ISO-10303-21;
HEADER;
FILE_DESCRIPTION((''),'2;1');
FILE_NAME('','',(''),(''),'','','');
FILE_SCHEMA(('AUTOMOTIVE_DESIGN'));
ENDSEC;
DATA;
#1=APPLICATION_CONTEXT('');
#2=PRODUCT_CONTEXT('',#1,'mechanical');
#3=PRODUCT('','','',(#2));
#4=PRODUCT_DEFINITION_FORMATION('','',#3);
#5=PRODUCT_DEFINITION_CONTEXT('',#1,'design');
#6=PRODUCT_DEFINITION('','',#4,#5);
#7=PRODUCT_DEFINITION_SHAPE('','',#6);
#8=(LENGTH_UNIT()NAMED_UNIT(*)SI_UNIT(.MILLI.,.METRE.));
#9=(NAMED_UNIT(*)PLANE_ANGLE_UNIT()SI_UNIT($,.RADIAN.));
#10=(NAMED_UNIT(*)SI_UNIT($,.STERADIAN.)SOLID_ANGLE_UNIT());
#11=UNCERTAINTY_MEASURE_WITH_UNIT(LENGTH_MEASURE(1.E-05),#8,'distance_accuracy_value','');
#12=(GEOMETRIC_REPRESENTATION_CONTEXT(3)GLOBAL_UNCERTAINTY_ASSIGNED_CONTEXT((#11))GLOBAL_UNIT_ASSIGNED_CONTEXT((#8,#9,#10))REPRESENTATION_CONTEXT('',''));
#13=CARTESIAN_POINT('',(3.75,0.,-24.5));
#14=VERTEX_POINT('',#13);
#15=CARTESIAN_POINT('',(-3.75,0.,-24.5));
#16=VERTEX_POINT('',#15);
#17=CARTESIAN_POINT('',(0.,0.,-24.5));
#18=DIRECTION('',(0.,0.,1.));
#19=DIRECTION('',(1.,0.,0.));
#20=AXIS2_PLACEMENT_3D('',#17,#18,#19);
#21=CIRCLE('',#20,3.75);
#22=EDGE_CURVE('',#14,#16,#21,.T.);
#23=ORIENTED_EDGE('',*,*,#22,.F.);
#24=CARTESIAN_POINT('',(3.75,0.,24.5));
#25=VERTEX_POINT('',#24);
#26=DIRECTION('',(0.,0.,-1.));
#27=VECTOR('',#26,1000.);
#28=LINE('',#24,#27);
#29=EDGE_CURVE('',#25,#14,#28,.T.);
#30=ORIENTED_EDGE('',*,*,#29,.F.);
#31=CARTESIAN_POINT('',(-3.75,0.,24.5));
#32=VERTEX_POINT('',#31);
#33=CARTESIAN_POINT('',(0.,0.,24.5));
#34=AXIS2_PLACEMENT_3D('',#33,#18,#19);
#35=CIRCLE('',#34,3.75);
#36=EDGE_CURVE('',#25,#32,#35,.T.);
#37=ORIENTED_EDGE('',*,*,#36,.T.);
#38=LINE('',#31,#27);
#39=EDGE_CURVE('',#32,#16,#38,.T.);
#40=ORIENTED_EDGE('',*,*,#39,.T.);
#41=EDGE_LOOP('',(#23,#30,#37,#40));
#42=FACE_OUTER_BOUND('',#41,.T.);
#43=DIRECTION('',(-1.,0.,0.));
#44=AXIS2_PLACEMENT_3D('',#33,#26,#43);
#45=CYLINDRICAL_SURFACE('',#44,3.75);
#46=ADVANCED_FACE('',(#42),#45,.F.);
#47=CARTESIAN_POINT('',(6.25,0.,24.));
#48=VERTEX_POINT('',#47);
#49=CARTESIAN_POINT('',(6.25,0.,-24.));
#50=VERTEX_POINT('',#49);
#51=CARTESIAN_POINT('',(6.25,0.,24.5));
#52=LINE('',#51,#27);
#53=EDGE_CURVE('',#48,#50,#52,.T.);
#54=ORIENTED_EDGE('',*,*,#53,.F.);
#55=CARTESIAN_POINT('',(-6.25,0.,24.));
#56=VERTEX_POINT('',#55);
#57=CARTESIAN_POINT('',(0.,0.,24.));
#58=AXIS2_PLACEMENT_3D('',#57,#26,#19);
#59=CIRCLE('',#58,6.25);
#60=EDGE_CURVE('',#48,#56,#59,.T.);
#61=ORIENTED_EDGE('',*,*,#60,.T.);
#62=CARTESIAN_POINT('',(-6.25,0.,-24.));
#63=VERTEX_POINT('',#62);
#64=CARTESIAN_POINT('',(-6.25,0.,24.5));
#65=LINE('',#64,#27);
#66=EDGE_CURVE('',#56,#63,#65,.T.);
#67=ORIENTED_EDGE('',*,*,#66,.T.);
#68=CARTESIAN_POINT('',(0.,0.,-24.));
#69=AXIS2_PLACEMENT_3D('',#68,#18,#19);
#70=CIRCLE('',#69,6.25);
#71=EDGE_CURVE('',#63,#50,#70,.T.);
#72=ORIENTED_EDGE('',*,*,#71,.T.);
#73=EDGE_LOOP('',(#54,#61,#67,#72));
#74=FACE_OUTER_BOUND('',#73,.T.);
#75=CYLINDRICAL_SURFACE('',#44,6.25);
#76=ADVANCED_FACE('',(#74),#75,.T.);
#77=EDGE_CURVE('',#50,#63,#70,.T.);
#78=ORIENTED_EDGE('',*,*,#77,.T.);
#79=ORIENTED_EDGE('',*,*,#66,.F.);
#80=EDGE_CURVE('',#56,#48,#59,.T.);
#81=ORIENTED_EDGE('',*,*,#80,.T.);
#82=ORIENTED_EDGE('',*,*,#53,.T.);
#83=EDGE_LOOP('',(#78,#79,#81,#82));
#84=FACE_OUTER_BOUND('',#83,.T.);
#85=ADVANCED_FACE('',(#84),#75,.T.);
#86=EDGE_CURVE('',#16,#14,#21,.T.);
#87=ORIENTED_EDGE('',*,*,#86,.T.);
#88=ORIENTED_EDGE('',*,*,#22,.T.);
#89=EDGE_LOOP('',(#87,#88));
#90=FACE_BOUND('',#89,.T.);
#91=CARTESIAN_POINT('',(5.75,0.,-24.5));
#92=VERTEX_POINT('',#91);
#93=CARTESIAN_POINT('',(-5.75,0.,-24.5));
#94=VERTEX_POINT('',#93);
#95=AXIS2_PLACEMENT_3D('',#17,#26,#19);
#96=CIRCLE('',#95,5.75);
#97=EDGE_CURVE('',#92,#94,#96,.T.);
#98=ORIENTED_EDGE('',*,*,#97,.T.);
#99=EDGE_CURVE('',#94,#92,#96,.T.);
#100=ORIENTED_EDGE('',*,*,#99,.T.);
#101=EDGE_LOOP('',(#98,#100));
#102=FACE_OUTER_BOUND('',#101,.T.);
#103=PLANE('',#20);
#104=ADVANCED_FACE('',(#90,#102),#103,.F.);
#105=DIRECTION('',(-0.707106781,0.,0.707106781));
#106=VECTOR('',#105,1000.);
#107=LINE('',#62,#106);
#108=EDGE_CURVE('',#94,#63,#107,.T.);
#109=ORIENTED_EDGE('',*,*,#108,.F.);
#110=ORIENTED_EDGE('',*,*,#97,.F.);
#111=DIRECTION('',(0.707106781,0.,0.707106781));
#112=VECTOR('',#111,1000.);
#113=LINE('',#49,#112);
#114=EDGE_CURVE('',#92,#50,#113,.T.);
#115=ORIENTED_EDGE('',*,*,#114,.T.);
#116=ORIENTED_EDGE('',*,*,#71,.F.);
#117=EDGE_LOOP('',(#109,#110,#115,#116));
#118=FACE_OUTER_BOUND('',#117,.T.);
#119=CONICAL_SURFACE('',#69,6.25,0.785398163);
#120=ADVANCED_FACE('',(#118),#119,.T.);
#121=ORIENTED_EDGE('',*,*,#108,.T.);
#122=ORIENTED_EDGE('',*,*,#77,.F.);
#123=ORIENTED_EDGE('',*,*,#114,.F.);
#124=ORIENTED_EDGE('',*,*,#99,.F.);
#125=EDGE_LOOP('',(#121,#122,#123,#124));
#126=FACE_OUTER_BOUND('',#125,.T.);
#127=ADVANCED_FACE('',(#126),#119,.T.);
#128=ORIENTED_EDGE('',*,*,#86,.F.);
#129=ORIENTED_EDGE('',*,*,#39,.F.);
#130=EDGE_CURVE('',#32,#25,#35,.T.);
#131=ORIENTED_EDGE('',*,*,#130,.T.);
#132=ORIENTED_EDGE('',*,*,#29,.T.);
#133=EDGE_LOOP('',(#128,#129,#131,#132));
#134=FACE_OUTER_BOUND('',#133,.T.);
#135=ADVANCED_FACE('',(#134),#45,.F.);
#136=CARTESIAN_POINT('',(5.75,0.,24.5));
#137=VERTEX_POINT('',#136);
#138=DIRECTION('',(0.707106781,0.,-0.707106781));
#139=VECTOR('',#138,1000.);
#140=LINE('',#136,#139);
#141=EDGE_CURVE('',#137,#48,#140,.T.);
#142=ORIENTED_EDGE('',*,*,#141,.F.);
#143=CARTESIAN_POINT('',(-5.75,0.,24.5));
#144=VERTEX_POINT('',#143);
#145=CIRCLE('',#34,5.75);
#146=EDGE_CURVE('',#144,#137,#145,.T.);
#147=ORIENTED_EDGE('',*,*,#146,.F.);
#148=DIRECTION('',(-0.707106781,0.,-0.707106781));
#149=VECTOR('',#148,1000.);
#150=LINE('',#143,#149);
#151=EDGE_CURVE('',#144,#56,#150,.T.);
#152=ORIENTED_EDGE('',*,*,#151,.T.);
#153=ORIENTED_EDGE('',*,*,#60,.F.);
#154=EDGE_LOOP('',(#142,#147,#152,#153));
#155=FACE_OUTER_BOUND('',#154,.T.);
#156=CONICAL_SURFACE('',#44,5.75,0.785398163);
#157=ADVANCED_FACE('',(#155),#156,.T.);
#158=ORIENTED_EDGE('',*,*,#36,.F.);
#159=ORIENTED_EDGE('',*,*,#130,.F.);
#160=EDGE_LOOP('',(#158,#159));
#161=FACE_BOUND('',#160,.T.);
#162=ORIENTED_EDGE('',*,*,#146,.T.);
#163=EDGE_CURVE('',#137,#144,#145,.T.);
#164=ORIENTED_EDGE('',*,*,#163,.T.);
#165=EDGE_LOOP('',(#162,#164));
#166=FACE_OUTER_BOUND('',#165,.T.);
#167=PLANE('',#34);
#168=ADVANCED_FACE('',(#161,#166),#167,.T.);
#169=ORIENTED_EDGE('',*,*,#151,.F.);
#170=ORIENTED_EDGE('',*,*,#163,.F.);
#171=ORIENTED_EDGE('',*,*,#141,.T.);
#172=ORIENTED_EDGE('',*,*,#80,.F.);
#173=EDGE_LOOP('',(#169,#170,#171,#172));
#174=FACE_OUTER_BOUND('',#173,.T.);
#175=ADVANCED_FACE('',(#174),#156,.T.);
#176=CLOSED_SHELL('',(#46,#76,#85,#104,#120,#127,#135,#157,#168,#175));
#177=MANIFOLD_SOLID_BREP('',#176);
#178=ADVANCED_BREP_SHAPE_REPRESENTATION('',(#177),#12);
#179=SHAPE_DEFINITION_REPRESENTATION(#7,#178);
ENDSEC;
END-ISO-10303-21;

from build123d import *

# Parameters (mm, degrees)
PIN_OD_PROFILE_12_5_R        = 6.25
PIN_OD_PROFILE_12_5_R_2      = 3.75
PIN_TUBE_L49_WALL_2_5_DEPTH  = 24.5
PIN_EDGE_CHAMFER_0_5X45_SIZE = 0.5


with BuildPart() as part:
    # Pin OD Profile Ø12.5 → Pin Tube L49 Wall 2.5 (new, symmetric)
    with BuildSketch(Plane.XY):
        Circle(PIN_OD_PROFILE_12_5_R)
        Circle(PIN_OD_PROFILE_12_5_R_2, mode=Mode.SUBTRACT)
    extrude(amount=PIN_TUBE_L49_WALL_2_5_DEPTH, both=True)

    # Pin Edge Chamfer 0.5x45°
    pin_edge_chamfer_0_5x45_edges = [part.edges().sort_by_distance(p)[0] for p in [
        (-6.25, 0, -24.5),
        (-6.25, 0, 24.5),
    ]]
    chamfer(pin_edge_chamfer_0_5x45_edges, length=PIN_EDGE_CHAMFER_0_5X45_SIZE)


solid = part.part
